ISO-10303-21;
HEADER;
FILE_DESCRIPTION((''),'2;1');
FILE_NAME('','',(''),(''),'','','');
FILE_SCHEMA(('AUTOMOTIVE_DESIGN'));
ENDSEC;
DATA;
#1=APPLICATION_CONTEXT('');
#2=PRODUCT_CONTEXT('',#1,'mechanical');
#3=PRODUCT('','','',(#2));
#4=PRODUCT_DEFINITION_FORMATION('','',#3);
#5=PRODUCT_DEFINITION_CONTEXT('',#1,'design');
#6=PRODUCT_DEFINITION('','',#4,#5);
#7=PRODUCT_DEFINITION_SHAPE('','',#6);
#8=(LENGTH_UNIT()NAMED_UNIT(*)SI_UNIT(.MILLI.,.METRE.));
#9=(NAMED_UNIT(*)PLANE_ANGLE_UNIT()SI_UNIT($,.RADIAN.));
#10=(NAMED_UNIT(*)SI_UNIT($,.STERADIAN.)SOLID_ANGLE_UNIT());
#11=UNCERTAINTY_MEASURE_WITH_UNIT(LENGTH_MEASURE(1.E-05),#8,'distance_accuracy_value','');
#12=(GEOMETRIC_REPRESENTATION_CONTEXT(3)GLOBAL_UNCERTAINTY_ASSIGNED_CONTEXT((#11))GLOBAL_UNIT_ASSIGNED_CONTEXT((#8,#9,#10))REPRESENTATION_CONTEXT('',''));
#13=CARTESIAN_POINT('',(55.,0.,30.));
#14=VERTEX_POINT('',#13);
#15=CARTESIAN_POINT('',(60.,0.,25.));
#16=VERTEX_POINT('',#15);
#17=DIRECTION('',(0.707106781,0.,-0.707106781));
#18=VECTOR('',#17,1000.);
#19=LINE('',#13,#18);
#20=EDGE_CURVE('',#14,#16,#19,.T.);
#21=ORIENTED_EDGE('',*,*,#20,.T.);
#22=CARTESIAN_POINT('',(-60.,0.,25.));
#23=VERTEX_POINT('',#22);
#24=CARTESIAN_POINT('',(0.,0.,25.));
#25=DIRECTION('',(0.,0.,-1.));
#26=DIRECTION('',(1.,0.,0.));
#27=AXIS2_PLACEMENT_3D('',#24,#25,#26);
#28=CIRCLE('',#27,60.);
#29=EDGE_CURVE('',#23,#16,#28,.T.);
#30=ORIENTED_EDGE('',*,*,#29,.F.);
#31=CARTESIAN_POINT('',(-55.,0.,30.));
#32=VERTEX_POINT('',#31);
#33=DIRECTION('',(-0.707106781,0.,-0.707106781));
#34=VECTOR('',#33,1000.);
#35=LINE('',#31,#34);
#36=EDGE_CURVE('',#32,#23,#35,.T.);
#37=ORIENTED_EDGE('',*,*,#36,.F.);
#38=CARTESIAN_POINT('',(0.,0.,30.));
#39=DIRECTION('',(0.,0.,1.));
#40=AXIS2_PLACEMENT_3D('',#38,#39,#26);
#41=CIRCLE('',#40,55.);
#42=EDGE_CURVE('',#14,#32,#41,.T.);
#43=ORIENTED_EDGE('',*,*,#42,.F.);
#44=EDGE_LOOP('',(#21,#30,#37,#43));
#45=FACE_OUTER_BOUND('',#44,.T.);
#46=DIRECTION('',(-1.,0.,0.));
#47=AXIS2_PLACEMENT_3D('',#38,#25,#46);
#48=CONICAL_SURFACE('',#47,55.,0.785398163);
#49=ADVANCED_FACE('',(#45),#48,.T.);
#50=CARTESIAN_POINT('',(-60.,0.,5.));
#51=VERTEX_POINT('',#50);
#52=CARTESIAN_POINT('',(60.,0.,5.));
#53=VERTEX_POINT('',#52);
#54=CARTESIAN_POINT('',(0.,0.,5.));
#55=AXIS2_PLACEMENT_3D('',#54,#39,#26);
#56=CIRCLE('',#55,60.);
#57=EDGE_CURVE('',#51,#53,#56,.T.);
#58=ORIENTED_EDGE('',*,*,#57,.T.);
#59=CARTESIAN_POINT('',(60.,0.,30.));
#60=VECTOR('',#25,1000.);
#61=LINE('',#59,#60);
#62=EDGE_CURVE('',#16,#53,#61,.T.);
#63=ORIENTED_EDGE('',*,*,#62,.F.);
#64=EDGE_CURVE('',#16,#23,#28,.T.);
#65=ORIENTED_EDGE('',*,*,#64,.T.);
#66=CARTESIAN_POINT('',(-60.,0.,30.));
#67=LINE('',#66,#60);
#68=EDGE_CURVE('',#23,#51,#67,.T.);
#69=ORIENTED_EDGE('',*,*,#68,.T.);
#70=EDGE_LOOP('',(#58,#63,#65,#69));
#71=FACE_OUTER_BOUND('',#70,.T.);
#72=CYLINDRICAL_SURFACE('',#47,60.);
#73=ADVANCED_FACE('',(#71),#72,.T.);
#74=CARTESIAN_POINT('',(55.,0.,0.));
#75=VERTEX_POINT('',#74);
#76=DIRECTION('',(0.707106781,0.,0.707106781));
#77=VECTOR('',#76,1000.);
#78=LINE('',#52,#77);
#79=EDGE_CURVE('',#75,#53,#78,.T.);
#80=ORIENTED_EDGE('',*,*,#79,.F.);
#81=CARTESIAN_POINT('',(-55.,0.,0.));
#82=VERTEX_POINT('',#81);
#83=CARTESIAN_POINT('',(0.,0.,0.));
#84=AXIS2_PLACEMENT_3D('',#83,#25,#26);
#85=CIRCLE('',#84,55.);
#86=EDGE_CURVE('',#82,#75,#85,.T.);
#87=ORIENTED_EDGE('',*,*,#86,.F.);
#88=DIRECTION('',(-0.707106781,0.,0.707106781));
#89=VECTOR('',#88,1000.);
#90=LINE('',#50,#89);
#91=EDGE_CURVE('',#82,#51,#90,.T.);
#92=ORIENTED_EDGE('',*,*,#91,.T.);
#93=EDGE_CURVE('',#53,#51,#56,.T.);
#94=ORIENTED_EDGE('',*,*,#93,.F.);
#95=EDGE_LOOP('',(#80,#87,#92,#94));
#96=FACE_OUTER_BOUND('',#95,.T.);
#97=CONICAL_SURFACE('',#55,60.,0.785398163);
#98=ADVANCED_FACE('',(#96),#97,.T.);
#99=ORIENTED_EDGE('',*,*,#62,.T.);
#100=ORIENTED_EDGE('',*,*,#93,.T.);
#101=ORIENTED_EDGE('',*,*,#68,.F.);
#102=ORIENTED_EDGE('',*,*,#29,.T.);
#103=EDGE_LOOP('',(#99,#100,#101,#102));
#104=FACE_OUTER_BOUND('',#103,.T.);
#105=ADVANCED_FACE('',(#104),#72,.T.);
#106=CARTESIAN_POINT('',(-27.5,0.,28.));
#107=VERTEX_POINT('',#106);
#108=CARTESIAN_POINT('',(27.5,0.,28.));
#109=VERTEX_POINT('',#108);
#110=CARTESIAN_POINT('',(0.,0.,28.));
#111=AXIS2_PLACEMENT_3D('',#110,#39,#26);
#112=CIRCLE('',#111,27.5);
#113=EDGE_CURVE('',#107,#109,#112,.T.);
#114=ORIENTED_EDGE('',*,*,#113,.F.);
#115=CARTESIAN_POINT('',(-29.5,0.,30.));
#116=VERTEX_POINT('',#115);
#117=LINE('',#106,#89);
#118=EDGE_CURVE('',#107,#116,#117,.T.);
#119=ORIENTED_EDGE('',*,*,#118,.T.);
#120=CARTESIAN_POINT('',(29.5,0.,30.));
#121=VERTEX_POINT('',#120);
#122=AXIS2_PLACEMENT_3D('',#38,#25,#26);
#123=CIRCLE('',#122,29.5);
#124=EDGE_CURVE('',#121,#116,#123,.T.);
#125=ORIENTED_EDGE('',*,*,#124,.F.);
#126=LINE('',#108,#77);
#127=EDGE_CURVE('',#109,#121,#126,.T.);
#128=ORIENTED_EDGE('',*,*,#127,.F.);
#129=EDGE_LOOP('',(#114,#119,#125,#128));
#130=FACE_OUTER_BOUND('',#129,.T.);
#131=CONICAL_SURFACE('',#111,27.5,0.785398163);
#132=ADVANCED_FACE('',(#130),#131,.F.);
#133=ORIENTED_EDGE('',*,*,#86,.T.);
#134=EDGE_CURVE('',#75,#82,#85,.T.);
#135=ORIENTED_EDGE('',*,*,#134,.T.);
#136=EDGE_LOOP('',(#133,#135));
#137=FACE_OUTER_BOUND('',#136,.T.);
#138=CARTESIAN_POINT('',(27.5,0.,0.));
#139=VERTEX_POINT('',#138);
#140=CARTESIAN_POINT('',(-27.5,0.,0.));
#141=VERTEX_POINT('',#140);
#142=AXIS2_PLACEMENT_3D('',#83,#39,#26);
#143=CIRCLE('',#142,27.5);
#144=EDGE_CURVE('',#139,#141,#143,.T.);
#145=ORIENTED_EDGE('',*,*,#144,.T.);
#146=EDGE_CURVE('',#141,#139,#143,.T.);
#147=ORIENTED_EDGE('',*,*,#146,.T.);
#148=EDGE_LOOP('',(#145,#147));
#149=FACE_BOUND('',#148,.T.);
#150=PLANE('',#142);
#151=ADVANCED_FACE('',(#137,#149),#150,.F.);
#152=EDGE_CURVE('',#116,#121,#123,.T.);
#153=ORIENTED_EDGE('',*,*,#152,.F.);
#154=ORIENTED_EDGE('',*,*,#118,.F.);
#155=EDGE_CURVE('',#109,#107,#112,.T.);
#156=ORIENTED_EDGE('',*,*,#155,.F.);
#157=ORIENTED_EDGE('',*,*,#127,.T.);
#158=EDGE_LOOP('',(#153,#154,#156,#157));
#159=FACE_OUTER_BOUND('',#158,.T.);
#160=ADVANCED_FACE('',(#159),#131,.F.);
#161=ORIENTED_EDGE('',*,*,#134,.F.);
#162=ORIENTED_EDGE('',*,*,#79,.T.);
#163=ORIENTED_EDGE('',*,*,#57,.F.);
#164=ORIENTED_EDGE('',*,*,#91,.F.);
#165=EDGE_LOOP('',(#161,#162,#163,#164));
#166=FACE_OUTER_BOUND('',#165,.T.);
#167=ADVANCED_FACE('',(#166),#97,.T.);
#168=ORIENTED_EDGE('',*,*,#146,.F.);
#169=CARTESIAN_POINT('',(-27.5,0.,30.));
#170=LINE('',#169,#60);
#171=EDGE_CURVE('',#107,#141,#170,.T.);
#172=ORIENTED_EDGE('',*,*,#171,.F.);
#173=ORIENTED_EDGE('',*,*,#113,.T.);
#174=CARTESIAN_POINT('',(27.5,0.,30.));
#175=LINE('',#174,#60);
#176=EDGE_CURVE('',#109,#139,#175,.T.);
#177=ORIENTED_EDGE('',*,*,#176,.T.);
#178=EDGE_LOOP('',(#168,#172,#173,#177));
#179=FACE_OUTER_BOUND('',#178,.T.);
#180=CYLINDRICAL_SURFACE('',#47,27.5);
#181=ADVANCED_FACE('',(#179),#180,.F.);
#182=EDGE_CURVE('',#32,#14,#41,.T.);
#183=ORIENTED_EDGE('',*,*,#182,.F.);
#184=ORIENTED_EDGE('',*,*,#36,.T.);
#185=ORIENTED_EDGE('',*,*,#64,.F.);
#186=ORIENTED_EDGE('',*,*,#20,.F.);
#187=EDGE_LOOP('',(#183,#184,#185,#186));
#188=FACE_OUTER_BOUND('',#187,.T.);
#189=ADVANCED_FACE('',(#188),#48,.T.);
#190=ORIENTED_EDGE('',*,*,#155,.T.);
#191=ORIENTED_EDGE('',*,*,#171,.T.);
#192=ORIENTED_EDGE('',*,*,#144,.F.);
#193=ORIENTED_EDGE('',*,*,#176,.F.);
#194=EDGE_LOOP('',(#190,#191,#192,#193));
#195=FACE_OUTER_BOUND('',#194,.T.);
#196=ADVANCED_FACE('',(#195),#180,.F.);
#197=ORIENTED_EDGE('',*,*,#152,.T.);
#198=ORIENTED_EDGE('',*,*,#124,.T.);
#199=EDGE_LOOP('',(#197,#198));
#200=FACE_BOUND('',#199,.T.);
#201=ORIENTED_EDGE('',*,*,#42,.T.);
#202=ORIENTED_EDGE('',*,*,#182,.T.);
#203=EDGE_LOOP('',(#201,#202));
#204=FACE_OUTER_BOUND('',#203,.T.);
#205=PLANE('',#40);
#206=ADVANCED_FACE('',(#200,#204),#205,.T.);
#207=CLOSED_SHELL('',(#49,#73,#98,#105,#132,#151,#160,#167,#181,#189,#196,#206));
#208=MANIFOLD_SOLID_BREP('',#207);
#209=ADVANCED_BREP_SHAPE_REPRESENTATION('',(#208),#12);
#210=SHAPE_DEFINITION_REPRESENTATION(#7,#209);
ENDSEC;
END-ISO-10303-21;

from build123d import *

# Parameters (mm, degrees)
SKETCH1_R           = 60
SKETCH1_R_2         = 27.5
BOSS_EXTRUDE1_DEPTH = 30
CHAMFER1_SIZE       = 5
CHAMFER2_SIZE       = 2


with BuildPart() as part:
    # Sketch1 → Boss-Extrude1 (new body)
    with BuildSketch(Plane.XY):
        Circle(SKETCH1_R)
        Circle(SKETCH1_R_2, mode=Mode.SUBTRACT)
    extrude(amount=BOSS_EXTRUDE1_DEPTH)

    # Chamfer1
    chamfer1_edges = [part.edges().sort_by_distance(p)[0] for p in [
        (-60, 0, 0),
        (-60, 0, 30),
    ]]
    chamfer(chamfer1_edges, length=CHAMFER1_SIZE)

    # Chamfer2
    chamfer2_edges = [part.edges().sort_by_distance(p)[0] for p in [
        (-27.5, 0, 30),
    ]]
    chamfer(chamfer2_edges, length=CHAMFER2_SIZE)


solid = part.part
